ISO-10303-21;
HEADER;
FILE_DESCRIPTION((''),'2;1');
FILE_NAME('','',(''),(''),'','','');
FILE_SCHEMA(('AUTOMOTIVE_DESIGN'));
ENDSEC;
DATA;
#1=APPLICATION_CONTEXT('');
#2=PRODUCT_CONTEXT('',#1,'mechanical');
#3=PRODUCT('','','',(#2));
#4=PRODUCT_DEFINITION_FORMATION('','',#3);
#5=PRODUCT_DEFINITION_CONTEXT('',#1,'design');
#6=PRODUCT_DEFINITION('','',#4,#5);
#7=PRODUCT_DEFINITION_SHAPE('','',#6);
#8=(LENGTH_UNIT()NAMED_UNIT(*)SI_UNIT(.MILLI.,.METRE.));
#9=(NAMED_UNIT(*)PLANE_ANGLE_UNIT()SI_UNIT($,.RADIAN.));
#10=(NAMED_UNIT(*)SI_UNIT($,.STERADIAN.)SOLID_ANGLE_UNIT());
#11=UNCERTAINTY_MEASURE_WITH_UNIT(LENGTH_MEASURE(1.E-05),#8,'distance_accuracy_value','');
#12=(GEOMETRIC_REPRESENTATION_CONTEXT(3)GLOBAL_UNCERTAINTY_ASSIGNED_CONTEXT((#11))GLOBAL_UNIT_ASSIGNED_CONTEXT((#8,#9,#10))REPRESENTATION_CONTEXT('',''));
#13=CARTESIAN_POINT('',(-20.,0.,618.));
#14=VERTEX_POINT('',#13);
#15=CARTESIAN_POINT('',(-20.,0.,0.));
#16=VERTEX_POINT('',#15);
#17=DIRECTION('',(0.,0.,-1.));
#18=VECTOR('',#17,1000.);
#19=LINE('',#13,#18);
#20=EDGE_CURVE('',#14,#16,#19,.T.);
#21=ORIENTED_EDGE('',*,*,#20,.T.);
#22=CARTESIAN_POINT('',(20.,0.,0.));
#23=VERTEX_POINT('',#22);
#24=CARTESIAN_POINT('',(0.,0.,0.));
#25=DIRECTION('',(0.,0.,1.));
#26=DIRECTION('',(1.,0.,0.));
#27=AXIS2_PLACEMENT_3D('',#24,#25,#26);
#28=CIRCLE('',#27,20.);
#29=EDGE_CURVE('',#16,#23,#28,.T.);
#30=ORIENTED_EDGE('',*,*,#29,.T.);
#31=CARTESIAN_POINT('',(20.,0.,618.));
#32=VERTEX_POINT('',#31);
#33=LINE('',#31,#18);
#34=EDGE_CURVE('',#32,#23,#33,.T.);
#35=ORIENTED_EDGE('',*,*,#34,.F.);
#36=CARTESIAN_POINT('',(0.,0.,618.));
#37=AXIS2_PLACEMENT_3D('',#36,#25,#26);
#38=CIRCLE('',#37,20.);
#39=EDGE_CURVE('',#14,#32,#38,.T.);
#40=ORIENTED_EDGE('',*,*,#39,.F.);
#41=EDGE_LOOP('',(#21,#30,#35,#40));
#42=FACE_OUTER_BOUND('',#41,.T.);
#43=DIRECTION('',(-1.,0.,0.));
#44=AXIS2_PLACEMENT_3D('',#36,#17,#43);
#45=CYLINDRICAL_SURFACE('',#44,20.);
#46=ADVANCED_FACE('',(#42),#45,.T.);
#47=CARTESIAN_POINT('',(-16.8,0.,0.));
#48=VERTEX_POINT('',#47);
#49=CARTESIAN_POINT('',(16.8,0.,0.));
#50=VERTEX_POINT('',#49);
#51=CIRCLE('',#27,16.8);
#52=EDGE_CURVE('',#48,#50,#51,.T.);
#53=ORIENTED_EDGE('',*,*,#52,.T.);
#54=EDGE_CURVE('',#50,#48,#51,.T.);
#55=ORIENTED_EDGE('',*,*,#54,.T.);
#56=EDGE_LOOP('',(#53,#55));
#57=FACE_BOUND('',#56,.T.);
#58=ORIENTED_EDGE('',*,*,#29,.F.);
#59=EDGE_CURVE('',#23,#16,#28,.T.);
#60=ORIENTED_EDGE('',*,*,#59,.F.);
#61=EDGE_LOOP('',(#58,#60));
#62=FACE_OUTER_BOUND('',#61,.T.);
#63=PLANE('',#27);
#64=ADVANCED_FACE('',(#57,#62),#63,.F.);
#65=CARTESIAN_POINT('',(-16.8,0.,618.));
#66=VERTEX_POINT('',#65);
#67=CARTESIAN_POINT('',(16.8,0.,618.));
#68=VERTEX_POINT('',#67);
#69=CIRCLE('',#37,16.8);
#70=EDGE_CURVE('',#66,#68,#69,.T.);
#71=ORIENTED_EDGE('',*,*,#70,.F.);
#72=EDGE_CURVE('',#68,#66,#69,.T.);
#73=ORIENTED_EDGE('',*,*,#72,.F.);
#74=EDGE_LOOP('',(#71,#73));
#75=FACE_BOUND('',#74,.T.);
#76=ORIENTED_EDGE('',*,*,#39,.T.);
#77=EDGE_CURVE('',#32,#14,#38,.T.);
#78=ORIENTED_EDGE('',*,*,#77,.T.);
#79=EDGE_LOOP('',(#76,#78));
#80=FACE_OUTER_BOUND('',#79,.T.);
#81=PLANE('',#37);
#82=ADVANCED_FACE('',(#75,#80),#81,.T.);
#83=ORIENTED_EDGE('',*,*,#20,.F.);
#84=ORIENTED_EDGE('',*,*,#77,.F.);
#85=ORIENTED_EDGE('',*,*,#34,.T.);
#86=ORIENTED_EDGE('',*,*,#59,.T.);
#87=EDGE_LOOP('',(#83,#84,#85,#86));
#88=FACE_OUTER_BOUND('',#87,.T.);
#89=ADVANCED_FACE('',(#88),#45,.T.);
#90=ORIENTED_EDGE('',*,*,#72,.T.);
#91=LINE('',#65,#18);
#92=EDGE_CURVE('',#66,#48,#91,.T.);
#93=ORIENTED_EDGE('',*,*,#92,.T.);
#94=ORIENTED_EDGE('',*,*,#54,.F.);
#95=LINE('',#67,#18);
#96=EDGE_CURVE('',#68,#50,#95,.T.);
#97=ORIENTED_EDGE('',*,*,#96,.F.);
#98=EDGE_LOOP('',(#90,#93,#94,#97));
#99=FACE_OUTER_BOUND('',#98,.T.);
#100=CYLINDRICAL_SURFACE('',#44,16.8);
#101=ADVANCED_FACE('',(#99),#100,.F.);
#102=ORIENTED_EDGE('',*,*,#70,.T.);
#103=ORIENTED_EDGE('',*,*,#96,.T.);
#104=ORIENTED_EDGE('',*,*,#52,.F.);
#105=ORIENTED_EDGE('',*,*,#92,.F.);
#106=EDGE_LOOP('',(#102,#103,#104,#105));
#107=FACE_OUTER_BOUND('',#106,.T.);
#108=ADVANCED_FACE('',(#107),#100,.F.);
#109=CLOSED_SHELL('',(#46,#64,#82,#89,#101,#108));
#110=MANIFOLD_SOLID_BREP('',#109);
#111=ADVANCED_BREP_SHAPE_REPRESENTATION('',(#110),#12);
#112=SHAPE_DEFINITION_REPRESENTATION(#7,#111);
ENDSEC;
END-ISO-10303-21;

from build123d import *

# Parameters (mm, degrees)
SKETCH_1_R      = 20
EXTRUDE_1_DEPTH = 618
SHELL_1_T       = -3.2


with BuildPart() as part:
    # 草图1 → 凸台-拉伸1 (new body)
    with BuildSketch(Plane.XY):
        Circle(SKETCH_1_R)
    extrude(amount=EXTRUDE_1_DEPTH)

    # 抽壳1
    shell_1_openings = [part.faces().sort_by_distance(p)[0] for p in [
        (0, 0, 618),
        (0, 0, 0),
    ]]
    offset(amount=SHELL_1_T, openings=shell_1_openings, kind=Kind.INTERSECTION)


solid = part.part
